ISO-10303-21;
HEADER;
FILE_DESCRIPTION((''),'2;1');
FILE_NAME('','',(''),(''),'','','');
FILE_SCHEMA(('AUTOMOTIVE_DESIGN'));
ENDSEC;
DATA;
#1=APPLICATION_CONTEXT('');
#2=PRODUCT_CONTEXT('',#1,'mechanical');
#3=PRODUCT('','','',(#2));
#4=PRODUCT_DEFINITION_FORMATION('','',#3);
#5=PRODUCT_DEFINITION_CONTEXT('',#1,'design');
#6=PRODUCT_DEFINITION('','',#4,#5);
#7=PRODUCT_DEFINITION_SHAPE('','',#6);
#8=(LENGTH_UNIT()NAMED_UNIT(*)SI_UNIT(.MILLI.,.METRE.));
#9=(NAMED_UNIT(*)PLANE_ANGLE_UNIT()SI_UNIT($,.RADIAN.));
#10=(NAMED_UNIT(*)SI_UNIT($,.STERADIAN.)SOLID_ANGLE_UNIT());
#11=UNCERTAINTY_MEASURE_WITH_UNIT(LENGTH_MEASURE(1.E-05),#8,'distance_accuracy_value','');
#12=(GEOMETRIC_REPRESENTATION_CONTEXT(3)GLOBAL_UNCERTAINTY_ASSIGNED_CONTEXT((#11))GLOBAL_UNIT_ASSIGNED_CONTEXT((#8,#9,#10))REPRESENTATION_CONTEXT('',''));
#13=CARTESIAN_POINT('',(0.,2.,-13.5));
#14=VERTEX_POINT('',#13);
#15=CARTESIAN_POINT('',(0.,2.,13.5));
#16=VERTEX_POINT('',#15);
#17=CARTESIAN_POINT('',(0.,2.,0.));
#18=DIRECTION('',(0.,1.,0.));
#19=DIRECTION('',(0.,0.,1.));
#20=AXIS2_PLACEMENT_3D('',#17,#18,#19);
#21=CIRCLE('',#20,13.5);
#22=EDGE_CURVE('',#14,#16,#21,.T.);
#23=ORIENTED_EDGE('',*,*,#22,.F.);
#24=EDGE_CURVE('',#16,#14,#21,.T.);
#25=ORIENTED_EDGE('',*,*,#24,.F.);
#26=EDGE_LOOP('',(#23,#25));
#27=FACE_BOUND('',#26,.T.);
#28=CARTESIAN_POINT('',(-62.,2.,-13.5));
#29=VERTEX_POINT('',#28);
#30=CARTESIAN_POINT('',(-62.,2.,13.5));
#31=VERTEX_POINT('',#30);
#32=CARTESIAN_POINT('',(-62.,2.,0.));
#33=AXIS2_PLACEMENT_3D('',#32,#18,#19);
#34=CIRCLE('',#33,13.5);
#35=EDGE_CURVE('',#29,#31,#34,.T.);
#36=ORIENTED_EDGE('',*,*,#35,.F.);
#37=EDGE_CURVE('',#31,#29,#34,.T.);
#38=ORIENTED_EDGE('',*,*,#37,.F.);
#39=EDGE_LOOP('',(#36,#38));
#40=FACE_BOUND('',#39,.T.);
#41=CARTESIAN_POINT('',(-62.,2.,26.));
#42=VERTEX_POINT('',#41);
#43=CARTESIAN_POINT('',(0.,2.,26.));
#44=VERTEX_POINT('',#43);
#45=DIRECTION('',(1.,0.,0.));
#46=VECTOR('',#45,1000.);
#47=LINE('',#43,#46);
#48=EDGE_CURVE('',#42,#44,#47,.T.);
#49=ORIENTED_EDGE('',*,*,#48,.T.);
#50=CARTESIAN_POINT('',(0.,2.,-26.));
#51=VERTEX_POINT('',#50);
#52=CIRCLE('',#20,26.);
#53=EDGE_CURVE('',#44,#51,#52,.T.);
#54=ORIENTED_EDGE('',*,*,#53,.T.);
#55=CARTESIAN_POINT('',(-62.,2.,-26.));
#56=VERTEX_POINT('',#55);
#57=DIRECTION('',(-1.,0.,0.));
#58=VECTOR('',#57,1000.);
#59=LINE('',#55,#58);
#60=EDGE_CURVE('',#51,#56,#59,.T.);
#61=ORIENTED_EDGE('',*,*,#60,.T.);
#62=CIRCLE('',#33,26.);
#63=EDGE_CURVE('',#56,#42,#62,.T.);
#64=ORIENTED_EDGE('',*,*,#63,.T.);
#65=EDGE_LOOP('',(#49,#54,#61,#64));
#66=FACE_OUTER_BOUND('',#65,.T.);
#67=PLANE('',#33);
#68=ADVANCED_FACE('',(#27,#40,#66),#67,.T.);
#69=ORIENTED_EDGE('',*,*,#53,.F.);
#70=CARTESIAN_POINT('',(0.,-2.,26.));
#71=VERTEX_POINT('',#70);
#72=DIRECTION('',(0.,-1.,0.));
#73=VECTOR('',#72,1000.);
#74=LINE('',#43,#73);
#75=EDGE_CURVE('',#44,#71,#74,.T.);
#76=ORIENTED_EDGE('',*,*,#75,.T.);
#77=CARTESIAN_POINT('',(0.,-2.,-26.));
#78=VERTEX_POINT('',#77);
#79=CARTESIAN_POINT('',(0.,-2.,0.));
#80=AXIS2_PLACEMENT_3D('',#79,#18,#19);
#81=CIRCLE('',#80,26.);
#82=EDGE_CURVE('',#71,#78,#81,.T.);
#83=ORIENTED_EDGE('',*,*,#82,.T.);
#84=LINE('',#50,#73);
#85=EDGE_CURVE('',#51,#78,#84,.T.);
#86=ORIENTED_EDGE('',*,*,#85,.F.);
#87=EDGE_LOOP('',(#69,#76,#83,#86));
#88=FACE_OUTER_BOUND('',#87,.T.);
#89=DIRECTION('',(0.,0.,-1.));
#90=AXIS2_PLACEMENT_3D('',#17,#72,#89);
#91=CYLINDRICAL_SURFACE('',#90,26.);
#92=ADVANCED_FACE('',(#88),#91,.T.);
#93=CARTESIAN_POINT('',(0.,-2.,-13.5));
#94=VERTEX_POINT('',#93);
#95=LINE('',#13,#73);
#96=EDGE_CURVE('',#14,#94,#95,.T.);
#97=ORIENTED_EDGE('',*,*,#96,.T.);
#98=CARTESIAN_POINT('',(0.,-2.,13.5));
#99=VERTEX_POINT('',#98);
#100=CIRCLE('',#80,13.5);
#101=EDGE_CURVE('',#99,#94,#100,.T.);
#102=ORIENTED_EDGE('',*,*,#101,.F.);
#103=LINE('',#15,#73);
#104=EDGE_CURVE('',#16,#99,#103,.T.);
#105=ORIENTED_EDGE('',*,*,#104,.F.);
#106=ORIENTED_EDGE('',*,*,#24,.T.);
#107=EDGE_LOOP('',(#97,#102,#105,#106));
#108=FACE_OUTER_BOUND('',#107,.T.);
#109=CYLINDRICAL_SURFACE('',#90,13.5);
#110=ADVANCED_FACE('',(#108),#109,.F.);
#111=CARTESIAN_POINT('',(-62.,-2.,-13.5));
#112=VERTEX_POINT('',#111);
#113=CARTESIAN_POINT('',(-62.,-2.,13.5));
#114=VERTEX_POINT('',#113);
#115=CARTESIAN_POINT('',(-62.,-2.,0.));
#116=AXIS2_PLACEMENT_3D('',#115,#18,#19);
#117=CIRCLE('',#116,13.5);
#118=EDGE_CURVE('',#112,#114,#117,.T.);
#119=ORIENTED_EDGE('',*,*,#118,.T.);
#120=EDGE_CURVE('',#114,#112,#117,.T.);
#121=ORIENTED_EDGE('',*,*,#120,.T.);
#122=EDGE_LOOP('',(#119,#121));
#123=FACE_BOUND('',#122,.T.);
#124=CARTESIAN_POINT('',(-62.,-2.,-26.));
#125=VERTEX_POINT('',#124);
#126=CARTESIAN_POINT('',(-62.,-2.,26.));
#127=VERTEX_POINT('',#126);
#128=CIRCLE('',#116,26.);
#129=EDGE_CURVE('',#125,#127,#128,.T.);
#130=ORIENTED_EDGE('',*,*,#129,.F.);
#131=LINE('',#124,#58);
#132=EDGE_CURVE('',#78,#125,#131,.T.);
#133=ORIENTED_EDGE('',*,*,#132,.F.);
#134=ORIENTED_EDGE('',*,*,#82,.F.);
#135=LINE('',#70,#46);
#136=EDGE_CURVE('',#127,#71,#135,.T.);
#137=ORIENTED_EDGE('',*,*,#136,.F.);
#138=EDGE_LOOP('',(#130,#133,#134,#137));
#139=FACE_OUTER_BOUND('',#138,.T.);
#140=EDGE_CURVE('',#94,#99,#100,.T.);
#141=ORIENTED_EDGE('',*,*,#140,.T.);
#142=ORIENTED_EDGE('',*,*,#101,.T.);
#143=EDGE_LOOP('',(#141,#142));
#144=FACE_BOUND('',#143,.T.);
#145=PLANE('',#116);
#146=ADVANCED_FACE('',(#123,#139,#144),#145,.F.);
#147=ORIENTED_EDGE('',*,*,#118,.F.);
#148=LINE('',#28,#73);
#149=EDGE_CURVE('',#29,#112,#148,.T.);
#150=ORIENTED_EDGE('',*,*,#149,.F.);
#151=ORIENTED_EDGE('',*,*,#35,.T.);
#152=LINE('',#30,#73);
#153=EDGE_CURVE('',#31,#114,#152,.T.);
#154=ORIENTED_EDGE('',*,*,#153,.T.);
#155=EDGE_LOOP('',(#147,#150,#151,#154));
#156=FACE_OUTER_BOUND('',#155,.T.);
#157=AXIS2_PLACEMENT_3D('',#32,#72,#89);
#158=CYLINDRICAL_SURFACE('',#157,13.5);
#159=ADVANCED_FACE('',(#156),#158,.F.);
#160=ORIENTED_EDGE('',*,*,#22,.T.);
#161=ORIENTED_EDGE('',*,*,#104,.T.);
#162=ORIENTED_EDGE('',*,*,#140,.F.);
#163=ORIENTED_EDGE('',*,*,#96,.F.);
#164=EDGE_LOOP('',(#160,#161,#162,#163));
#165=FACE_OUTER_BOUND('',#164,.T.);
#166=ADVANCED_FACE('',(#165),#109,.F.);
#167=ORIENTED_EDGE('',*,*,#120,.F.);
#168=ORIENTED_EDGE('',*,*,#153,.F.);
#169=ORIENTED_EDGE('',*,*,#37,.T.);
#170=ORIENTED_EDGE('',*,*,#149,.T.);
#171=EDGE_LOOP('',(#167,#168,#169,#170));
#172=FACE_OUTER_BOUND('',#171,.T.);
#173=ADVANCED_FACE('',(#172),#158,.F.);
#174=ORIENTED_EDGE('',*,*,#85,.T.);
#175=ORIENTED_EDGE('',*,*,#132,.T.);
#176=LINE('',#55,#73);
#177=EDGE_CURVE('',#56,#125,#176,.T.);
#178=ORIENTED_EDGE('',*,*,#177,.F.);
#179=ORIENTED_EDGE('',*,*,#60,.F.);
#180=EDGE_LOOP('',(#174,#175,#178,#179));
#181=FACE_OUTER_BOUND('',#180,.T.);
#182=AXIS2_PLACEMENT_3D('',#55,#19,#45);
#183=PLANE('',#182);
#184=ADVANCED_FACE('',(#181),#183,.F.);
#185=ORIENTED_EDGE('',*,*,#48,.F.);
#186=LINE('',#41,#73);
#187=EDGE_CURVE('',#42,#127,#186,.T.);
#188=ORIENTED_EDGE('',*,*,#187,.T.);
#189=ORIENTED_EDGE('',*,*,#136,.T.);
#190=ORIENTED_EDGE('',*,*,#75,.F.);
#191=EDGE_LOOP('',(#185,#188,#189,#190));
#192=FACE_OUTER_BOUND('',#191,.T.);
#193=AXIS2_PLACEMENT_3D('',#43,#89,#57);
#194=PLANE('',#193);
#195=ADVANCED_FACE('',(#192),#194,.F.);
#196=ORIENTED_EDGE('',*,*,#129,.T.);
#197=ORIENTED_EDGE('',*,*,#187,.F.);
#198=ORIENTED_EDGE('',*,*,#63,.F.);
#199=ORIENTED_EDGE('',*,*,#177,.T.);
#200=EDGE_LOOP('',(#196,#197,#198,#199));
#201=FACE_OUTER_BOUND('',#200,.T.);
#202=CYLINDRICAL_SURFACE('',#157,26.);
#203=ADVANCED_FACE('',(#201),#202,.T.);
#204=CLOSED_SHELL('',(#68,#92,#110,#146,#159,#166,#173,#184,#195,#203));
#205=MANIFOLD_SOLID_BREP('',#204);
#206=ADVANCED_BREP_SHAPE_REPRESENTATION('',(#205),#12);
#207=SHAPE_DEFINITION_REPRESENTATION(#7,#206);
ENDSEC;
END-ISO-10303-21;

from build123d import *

# Parameters (mm, degrees)
SKETCH1_R      = 13.5
EXTRUDE1_DEPTH = 2


with BuildPart() as part:
    # Sketch1 → Extrude1 (new, symmetric)
    with BuildSketch(Plane(origin=(0, 0, 0), x_dir=(1, 0, 0), z_dir=(0, 1, 0))):
        with BuildLine():
            Line((-62, 26), (0, 26))
            ThreePointArc((0, 26), (26, 0), (0, -26))
            Line((0, -26), (-62, -26))
            ThreePointArc((-62, -26), (-88, 0), (-62, 26))
        make_face()
        with Locations(Location((0, 0, 0), (0, 0, 270))):
            Circle(SKETCH1_R, mode=Mode.SUBTRACT)
        with Locations(Location((-62, 0, 0), (0, 0, 270))):
            Circle(SKETCH1_R, mode=Mode.SUBTRACT)
    extrude(amount=EXTRUDE1_DEPTH, both=True)


solid = part.part
